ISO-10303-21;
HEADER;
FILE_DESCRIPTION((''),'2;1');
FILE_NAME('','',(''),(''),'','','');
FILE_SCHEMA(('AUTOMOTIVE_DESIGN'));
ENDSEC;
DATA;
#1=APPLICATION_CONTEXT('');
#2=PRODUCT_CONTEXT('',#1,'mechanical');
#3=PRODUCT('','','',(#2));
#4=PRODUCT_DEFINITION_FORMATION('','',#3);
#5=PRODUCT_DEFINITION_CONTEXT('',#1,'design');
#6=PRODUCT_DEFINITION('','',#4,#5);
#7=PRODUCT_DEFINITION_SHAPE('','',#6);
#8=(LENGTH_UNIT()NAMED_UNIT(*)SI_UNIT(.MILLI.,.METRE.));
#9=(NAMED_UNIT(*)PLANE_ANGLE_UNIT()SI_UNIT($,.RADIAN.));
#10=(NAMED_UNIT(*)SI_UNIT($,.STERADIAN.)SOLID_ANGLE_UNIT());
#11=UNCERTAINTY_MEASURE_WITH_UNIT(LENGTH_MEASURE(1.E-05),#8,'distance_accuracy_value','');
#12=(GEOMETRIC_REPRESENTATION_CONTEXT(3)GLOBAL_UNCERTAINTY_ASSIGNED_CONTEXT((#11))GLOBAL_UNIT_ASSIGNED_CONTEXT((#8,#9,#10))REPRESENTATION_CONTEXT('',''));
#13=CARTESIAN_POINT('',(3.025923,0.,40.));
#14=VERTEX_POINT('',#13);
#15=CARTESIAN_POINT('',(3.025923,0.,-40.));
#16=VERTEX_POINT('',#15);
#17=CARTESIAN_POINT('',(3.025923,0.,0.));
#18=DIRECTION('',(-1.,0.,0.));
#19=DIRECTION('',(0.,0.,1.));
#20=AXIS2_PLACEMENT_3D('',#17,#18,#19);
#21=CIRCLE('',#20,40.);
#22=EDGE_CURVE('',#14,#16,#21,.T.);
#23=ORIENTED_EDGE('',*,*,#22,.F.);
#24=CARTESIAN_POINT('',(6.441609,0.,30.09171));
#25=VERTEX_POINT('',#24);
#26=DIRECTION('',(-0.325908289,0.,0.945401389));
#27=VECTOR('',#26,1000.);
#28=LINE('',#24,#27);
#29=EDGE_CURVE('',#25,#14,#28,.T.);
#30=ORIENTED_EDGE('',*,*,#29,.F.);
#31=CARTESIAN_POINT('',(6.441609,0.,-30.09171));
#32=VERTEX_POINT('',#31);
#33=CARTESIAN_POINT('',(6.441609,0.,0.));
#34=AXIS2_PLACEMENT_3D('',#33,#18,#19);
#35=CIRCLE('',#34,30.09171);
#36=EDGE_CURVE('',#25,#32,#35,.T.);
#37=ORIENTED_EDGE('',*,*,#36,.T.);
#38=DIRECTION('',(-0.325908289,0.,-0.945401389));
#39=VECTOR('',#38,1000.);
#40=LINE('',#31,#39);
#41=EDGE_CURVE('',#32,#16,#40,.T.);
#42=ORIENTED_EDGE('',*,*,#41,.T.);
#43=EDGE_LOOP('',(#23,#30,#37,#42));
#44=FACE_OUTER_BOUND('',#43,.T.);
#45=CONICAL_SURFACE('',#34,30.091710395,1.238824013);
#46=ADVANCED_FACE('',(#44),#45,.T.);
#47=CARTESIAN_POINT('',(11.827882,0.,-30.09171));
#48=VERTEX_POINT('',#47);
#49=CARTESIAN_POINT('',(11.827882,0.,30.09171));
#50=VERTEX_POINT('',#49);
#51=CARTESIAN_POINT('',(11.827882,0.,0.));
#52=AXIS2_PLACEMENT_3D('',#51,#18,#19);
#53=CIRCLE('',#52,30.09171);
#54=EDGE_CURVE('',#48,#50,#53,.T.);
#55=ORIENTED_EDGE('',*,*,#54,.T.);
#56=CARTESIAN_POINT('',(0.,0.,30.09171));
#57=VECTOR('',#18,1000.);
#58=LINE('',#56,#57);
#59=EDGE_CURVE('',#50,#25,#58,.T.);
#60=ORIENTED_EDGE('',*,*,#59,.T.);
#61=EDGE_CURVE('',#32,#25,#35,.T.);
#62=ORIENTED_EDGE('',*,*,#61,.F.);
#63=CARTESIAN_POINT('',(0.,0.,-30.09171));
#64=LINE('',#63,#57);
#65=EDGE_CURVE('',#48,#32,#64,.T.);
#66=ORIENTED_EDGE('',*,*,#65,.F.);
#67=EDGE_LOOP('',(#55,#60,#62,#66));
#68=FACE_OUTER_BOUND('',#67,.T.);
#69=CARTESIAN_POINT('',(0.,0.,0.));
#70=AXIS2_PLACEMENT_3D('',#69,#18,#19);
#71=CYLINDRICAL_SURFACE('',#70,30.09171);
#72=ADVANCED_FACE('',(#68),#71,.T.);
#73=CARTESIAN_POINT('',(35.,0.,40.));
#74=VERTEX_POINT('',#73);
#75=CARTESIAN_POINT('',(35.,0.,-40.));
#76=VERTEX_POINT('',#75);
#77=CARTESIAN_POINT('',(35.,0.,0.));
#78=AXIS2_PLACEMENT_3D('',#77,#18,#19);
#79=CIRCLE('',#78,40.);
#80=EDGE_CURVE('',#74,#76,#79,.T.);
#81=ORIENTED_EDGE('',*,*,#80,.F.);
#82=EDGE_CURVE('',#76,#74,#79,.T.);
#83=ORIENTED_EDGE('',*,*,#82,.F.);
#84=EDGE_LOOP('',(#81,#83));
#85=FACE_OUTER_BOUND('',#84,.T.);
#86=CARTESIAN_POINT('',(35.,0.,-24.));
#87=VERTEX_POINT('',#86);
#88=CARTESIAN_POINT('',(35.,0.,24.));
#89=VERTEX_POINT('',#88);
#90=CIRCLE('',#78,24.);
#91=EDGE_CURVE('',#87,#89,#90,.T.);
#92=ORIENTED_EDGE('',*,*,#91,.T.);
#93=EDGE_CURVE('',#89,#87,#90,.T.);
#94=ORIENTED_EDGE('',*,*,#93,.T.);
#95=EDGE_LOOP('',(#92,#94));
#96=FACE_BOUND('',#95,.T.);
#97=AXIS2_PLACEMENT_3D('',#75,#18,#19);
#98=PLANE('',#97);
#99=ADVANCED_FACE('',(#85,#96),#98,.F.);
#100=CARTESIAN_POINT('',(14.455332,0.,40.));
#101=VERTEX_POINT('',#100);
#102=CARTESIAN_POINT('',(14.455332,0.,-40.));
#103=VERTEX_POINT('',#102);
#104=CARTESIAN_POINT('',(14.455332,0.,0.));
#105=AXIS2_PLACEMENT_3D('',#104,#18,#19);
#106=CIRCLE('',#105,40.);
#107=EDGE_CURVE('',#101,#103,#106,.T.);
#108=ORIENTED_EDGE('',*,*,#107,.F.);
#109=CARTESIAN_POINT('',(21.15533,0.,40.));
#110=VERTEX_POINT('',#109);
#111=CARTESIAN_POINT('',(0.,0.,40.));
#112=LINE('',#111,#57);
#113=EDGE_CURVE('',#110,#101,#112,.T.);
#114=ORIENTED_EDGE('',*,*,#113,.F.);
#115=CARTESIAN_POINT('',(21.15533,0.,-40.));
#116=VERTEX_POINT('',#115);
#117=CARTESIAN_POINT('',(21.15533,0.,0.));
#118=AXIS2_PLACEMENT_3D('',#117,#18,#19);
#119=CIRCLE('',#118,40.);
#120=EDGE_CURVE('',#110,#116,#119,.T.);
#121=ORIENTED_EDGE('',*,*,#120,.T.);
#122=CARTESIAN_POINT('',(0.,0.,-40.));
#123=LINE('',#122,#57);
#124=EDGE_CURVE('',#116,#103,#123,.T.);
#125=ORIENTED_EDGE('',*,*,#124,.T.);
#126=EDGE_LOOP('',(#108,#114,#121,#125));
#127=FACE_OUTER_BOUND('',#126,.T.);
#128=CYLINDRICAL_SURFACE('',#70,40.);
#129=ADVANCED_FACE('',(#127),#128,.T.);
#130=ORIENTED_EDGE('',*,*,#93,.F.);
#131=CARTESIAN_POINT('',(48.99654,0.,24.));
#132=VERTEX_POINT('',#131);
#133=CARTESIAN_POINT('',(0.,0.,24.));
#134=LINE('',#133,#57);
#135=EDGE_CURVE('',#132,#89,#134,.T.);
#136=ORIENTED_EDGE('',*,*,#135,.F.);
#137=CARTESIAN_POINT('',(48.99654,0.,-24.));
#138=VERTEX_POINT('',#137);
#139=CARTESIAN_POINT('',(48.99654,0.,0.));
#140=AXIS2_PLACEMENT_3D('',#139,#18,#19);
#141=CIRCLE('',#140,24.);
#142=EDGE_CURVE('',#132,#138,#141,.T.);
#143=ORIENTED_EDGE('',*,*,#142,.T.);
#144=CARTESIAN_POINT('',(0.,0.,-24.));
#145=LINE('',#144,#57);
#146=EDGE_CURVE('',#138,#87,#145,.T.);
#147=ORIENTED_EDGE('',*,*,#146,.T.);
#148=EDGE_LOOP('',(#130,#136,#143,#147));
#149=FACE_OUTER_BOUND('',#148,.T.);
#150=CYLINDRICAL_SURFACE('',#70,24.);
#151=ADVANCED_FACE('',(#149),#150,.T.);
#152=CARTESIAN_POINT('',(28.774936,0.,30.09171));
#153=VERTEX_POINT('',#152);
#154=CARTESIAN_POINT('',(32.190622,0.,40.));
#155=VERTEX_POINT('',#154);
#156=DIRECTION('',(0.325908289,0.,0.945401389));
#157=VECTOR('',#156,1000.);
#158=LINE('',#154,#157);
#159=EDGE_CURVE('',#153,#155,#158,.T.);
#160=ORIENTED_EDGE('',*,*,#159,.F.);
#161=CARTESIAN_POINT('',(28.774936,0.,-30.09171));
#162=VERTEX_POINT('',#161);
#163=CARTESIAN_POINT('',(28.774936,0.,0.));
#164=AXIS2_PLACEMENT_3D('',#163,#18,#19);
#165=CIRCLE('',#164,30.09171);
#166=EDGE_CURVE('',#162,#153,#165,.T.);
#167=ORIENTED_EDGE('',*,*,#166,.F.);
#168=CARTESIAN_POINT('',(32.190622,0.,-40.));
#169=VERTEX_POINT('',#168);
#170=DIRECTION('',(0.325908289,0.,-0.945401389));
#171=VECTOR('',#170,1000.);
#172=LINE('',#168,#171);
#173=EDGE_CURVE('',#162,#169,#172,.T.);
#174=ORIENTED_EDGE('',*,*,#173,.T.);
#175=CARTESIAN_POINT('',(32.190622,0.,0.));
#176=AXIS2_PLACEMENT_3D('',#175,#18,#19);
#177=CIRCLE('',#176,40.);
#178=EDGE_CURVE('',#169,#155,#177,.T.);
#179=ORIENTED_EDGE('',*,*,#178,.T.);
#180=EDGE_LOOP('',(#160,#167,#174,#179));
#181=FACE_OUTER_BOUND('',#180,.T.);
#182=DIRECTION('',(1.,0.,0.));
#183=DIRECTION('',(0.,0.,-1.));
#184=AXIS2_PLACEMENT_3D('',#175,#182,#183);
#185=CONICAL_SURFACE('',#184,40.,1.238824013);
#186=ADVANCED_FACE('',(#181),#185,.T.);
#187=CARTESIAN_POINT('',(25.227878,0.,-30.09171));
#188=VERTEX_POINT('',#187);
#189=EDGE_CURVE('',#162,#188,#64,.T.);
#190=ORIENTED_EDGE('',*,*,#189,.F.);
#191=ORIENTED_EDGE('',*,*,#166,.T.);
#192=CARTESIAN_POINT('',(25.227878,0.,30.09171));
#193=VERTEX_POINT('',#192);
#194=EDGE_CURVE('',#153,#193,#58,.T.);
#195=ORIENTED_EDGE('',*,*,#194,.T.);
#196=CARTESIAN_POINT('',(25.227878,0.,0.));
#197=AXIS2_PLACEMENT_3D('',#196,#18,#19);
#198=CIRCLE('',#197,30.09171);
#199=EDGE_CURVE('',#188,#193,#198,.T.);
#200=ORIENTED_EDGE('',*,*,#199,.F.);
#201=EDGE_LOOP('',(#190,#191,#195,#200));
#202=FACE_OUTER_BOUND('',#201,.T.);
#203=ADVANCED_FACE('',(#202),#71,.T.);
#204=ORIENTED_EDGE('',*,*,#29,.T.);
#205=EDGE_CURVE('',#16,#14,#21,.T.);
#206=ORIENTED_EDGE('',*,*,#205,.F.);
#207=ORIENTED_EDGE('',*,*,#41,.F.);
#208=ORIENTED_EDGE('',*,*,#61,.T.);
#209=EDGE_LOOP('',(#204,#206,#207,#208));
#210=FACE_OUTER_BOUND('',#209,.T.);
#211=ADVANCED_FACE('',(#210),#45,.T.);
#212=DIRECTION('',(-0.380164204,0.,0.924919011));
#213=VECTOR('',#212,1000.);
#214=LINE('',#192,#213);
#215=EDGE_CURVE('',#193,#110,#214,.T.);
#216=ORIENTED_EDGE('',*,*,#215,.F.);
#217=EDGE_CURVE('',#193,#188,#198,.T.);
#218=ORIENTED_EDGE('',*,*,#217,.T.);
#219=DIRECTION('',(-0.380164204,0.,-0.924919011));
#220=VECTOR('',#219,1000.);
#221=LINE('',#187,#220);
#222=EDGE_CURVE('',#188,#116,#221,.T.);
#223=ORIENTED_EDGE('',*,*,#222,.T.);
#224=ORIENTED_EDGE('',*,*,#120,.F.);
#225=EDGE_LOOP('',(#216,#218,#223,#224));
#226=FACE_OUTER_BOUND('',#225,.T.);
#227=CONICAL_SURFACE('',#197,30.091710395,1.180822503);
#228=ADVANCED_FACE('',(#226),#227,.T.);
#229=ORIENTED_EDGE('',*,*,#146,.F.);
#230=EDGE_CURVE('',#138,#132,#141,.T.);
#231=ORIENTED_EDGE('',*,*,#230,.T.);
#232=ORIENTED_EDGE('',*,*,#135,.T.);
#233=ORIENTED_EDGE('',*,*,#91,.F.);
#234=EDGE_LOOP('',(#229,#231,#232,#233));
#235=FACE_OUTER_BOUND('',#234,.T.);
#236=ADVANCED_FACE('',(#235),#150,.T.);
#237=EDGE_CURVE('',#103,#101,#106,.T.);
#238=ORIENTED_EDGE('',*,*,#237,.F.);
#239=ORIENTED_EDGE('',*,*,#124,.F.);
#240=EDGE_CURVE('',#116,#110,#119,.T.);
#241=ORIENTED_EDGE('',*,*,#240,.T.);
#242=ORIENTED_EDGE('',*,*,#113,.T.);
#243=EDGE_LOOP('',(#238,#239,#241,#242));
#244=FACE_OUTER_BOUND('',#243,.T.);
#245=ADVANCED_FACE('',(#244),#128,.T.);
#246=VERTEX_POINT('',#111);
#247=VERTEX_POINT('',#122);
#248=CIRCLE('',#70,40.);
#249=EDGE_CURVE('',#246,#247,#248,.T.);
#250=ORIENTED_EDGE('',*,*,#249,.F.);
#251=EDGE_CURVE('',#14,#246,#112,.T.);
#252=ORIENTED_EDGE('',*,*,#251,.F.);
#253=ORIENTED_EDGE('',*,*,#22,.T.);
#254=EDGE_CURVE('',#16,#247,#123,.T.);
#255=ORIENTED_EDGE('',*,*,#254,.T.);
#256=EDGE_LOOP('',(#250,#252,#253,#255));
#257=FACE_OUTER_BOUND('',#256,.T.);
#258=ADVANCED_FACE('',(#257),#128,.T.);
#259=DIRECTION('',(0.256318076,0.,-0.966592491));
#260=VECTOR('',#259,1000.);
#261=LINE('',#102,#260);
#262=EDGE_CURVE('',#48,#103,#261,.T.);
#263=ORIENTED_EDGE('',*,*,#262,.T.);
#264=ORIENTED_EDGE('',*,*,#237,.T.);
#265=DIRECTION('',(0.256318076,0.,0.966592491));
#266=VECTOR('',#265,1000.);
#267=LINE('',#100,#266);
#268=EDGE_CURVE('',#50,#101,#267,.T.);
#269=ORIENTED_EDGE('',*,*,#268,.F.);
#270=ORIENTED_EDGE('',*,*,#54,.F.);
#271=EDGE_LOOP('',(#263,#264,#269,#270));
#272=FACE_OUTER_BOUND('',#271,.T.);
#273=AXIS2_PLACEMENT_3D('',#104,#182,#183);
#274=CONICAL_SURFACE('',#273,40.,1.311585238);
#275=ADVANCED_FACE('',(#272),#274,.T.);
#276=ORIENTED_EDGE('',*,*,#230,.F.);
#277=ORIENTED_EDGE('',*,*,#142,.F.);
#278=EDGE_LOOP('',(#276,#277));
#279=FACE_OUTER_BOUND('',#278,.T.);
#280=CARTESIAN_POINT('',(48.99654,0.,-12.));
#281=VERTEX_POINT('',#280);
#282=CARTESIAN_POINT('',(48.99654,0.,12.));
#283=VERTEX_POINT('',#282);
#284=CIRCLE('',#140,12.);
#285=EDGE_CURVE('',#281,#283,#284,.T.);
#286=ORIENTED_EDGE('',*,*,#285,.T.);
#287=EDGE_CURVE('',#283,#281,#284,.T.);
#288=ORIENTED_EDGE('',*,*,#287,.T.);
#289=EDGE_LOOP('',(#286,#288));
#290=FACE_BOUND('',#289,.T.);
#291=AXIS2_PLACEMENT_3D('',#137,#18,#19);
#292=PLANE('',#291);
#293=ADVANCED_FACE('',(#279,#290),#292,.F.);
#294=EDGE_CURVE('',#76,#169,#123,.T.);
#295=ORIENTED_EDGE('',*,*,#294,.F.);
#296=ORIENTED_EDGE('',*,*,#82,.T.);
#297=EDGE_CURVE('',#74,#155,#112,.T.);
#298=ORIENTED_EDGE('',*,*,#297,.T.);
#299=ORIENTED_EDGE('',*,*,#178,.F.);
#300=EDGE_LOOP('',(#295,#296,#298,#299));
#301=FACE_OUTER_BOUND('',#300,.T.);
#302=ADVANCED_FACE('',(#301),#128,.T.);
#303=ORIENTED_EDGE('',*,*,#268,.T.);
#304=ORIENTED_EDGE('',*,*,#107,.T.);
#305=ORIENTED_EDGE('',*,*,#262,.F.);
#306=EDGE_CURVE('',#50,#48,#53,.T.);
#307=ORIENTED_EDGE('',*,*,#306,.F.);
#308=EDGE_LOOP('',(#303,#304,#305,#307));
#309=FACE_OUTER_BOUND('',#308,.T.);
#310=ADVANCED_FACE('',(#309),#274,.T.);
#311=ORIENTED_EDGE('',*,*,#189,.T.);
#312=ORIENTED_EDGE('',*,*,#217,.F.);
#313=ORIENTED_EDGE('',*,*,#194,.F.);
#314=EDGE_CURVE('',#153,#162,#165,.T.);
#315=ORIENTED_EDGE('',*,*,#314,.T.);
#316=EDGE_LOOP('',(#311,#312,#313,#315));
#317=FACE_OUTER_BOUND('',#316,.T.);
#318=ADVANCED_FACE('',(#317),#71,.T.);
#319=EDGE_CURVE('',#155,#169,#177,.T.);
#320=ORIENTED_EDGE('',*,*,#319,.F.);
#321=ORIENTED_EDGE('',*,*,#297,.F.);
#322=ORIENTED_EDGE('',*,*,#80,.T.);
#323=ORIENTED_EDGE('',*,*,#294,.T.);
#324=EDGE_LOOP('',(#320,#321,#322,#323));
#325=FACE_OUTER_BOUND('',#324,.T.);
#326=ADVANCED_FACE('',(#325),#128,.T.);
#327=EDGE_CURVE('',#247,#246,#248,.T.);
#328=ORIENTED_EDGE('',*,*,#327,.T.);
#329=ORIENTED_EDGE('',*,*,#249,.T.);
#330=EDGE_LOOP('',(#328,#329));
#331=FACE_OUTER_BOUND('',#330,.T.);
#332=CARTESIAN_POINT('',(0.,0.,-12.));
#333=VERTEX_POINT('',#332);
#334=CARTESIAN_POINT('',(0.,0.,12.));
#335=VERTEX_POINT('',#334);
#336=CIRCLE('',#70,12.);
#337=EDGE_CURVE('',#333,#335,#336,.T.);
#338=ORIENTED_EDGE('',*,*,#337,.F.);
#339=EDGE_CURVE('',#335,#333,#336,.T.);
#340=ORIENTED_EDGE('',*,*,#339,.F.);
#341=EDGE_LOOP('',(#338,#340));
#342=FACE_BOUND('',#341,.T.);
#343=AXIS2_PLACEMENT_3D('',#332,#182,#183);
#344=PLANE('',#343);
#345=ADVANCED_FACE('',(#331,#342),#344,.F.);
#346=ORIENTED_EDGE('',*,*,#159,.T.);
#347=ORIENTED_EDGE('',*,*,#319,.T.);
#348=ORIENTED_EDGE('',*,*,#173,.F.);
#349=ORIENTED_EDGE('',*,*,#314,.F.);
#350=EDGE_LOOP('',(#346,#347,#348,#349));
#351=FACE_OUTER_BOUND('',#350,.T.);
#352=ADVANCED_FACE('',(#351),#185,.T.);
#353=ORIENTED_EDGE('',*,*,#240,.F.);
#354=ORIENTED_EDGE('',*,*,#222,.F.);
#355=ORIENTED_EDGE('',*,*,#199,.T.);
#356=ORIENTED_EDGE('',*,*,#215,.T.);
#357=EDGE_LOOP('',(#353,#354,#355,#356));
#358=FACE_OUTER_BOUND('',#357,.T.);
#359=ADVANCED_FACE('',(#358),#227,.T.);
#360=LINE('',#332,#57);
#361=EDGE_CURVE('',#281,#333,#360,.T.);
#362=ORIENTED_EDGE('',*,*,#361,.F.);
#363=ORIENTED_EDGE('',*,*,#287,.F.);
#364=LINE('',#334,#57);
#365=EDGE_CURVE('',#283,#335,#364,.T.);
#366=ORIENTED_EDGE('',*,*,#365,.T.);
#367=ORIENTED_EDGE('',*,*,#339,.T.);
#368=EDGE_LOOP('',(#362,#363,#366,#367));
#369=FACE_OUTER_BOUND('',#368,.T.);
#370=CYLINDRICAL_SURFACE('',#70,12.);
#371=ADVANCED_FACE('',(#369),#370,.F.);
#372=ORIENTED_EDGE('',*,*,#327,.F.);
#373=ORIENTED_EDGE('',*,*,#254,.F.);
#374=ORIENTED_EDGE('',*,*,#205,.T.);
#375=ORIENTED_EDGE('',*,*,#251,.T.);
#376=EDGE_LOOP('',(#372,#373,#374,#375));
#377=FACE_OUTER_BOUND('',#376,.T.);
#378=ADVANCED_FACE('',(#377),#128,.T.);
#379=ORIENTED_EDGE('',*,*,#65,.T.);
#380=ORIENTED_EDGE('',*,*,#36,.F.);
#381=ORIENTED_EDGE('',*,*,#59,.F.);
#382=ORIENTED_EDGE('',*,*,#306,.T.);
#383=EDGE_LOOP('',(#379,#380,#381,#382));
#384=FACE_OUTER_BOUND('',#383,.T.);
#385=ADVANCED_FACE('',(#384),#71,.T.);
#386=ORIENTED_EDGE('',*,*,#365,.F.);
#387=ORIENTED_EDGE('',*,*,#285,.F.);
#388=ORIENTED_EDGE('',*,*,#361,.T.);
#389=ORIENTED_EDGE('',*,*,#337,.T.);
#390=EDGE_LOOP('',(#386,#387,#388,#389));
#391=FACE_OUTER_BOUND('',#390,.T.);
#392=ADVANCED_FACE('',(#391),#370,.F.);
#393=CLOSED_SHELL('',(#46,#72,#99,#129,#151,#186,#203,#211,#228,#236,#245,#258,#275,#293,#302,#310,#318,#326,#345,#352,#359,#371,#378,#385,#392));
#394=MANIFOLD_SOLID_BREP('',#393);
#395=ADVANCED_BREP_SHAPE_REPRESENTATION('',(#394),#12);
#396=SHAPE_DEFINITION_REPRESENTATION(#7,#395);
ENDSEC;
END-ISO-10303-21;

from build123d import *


with BuildPart() as part:
    # Sketch1 → Revolve1 (revolve)
    with BuildSketch(Plane(origin=(0, 0, 0), x_dir=(1, 0, 0), z_dir=(0, 1, 0)), mode=Mode.PRIVATE) as revolve1_sk:
        Polygon((0, 12), (0, 40), (3.025923231, 40), (6.441608618, 30.091710395), (11.827881728, 30.091710395), (14.455332026, 40), (21.155330284, 40), (25.227878246, 30.091710395), (28.774936147, 30.091710395), (32.190621534, 40), (35, 40), (35, 24), (48.996539792, 24), (48.996539792, 12), align=None)
    revolve(revolve1_sk.sketch.rotate(Axis((0, 0, 0), (1, 0, 0)), 180), axis=Axis((0, 0, 0), (1, 0, 0)))


solid = part.part
